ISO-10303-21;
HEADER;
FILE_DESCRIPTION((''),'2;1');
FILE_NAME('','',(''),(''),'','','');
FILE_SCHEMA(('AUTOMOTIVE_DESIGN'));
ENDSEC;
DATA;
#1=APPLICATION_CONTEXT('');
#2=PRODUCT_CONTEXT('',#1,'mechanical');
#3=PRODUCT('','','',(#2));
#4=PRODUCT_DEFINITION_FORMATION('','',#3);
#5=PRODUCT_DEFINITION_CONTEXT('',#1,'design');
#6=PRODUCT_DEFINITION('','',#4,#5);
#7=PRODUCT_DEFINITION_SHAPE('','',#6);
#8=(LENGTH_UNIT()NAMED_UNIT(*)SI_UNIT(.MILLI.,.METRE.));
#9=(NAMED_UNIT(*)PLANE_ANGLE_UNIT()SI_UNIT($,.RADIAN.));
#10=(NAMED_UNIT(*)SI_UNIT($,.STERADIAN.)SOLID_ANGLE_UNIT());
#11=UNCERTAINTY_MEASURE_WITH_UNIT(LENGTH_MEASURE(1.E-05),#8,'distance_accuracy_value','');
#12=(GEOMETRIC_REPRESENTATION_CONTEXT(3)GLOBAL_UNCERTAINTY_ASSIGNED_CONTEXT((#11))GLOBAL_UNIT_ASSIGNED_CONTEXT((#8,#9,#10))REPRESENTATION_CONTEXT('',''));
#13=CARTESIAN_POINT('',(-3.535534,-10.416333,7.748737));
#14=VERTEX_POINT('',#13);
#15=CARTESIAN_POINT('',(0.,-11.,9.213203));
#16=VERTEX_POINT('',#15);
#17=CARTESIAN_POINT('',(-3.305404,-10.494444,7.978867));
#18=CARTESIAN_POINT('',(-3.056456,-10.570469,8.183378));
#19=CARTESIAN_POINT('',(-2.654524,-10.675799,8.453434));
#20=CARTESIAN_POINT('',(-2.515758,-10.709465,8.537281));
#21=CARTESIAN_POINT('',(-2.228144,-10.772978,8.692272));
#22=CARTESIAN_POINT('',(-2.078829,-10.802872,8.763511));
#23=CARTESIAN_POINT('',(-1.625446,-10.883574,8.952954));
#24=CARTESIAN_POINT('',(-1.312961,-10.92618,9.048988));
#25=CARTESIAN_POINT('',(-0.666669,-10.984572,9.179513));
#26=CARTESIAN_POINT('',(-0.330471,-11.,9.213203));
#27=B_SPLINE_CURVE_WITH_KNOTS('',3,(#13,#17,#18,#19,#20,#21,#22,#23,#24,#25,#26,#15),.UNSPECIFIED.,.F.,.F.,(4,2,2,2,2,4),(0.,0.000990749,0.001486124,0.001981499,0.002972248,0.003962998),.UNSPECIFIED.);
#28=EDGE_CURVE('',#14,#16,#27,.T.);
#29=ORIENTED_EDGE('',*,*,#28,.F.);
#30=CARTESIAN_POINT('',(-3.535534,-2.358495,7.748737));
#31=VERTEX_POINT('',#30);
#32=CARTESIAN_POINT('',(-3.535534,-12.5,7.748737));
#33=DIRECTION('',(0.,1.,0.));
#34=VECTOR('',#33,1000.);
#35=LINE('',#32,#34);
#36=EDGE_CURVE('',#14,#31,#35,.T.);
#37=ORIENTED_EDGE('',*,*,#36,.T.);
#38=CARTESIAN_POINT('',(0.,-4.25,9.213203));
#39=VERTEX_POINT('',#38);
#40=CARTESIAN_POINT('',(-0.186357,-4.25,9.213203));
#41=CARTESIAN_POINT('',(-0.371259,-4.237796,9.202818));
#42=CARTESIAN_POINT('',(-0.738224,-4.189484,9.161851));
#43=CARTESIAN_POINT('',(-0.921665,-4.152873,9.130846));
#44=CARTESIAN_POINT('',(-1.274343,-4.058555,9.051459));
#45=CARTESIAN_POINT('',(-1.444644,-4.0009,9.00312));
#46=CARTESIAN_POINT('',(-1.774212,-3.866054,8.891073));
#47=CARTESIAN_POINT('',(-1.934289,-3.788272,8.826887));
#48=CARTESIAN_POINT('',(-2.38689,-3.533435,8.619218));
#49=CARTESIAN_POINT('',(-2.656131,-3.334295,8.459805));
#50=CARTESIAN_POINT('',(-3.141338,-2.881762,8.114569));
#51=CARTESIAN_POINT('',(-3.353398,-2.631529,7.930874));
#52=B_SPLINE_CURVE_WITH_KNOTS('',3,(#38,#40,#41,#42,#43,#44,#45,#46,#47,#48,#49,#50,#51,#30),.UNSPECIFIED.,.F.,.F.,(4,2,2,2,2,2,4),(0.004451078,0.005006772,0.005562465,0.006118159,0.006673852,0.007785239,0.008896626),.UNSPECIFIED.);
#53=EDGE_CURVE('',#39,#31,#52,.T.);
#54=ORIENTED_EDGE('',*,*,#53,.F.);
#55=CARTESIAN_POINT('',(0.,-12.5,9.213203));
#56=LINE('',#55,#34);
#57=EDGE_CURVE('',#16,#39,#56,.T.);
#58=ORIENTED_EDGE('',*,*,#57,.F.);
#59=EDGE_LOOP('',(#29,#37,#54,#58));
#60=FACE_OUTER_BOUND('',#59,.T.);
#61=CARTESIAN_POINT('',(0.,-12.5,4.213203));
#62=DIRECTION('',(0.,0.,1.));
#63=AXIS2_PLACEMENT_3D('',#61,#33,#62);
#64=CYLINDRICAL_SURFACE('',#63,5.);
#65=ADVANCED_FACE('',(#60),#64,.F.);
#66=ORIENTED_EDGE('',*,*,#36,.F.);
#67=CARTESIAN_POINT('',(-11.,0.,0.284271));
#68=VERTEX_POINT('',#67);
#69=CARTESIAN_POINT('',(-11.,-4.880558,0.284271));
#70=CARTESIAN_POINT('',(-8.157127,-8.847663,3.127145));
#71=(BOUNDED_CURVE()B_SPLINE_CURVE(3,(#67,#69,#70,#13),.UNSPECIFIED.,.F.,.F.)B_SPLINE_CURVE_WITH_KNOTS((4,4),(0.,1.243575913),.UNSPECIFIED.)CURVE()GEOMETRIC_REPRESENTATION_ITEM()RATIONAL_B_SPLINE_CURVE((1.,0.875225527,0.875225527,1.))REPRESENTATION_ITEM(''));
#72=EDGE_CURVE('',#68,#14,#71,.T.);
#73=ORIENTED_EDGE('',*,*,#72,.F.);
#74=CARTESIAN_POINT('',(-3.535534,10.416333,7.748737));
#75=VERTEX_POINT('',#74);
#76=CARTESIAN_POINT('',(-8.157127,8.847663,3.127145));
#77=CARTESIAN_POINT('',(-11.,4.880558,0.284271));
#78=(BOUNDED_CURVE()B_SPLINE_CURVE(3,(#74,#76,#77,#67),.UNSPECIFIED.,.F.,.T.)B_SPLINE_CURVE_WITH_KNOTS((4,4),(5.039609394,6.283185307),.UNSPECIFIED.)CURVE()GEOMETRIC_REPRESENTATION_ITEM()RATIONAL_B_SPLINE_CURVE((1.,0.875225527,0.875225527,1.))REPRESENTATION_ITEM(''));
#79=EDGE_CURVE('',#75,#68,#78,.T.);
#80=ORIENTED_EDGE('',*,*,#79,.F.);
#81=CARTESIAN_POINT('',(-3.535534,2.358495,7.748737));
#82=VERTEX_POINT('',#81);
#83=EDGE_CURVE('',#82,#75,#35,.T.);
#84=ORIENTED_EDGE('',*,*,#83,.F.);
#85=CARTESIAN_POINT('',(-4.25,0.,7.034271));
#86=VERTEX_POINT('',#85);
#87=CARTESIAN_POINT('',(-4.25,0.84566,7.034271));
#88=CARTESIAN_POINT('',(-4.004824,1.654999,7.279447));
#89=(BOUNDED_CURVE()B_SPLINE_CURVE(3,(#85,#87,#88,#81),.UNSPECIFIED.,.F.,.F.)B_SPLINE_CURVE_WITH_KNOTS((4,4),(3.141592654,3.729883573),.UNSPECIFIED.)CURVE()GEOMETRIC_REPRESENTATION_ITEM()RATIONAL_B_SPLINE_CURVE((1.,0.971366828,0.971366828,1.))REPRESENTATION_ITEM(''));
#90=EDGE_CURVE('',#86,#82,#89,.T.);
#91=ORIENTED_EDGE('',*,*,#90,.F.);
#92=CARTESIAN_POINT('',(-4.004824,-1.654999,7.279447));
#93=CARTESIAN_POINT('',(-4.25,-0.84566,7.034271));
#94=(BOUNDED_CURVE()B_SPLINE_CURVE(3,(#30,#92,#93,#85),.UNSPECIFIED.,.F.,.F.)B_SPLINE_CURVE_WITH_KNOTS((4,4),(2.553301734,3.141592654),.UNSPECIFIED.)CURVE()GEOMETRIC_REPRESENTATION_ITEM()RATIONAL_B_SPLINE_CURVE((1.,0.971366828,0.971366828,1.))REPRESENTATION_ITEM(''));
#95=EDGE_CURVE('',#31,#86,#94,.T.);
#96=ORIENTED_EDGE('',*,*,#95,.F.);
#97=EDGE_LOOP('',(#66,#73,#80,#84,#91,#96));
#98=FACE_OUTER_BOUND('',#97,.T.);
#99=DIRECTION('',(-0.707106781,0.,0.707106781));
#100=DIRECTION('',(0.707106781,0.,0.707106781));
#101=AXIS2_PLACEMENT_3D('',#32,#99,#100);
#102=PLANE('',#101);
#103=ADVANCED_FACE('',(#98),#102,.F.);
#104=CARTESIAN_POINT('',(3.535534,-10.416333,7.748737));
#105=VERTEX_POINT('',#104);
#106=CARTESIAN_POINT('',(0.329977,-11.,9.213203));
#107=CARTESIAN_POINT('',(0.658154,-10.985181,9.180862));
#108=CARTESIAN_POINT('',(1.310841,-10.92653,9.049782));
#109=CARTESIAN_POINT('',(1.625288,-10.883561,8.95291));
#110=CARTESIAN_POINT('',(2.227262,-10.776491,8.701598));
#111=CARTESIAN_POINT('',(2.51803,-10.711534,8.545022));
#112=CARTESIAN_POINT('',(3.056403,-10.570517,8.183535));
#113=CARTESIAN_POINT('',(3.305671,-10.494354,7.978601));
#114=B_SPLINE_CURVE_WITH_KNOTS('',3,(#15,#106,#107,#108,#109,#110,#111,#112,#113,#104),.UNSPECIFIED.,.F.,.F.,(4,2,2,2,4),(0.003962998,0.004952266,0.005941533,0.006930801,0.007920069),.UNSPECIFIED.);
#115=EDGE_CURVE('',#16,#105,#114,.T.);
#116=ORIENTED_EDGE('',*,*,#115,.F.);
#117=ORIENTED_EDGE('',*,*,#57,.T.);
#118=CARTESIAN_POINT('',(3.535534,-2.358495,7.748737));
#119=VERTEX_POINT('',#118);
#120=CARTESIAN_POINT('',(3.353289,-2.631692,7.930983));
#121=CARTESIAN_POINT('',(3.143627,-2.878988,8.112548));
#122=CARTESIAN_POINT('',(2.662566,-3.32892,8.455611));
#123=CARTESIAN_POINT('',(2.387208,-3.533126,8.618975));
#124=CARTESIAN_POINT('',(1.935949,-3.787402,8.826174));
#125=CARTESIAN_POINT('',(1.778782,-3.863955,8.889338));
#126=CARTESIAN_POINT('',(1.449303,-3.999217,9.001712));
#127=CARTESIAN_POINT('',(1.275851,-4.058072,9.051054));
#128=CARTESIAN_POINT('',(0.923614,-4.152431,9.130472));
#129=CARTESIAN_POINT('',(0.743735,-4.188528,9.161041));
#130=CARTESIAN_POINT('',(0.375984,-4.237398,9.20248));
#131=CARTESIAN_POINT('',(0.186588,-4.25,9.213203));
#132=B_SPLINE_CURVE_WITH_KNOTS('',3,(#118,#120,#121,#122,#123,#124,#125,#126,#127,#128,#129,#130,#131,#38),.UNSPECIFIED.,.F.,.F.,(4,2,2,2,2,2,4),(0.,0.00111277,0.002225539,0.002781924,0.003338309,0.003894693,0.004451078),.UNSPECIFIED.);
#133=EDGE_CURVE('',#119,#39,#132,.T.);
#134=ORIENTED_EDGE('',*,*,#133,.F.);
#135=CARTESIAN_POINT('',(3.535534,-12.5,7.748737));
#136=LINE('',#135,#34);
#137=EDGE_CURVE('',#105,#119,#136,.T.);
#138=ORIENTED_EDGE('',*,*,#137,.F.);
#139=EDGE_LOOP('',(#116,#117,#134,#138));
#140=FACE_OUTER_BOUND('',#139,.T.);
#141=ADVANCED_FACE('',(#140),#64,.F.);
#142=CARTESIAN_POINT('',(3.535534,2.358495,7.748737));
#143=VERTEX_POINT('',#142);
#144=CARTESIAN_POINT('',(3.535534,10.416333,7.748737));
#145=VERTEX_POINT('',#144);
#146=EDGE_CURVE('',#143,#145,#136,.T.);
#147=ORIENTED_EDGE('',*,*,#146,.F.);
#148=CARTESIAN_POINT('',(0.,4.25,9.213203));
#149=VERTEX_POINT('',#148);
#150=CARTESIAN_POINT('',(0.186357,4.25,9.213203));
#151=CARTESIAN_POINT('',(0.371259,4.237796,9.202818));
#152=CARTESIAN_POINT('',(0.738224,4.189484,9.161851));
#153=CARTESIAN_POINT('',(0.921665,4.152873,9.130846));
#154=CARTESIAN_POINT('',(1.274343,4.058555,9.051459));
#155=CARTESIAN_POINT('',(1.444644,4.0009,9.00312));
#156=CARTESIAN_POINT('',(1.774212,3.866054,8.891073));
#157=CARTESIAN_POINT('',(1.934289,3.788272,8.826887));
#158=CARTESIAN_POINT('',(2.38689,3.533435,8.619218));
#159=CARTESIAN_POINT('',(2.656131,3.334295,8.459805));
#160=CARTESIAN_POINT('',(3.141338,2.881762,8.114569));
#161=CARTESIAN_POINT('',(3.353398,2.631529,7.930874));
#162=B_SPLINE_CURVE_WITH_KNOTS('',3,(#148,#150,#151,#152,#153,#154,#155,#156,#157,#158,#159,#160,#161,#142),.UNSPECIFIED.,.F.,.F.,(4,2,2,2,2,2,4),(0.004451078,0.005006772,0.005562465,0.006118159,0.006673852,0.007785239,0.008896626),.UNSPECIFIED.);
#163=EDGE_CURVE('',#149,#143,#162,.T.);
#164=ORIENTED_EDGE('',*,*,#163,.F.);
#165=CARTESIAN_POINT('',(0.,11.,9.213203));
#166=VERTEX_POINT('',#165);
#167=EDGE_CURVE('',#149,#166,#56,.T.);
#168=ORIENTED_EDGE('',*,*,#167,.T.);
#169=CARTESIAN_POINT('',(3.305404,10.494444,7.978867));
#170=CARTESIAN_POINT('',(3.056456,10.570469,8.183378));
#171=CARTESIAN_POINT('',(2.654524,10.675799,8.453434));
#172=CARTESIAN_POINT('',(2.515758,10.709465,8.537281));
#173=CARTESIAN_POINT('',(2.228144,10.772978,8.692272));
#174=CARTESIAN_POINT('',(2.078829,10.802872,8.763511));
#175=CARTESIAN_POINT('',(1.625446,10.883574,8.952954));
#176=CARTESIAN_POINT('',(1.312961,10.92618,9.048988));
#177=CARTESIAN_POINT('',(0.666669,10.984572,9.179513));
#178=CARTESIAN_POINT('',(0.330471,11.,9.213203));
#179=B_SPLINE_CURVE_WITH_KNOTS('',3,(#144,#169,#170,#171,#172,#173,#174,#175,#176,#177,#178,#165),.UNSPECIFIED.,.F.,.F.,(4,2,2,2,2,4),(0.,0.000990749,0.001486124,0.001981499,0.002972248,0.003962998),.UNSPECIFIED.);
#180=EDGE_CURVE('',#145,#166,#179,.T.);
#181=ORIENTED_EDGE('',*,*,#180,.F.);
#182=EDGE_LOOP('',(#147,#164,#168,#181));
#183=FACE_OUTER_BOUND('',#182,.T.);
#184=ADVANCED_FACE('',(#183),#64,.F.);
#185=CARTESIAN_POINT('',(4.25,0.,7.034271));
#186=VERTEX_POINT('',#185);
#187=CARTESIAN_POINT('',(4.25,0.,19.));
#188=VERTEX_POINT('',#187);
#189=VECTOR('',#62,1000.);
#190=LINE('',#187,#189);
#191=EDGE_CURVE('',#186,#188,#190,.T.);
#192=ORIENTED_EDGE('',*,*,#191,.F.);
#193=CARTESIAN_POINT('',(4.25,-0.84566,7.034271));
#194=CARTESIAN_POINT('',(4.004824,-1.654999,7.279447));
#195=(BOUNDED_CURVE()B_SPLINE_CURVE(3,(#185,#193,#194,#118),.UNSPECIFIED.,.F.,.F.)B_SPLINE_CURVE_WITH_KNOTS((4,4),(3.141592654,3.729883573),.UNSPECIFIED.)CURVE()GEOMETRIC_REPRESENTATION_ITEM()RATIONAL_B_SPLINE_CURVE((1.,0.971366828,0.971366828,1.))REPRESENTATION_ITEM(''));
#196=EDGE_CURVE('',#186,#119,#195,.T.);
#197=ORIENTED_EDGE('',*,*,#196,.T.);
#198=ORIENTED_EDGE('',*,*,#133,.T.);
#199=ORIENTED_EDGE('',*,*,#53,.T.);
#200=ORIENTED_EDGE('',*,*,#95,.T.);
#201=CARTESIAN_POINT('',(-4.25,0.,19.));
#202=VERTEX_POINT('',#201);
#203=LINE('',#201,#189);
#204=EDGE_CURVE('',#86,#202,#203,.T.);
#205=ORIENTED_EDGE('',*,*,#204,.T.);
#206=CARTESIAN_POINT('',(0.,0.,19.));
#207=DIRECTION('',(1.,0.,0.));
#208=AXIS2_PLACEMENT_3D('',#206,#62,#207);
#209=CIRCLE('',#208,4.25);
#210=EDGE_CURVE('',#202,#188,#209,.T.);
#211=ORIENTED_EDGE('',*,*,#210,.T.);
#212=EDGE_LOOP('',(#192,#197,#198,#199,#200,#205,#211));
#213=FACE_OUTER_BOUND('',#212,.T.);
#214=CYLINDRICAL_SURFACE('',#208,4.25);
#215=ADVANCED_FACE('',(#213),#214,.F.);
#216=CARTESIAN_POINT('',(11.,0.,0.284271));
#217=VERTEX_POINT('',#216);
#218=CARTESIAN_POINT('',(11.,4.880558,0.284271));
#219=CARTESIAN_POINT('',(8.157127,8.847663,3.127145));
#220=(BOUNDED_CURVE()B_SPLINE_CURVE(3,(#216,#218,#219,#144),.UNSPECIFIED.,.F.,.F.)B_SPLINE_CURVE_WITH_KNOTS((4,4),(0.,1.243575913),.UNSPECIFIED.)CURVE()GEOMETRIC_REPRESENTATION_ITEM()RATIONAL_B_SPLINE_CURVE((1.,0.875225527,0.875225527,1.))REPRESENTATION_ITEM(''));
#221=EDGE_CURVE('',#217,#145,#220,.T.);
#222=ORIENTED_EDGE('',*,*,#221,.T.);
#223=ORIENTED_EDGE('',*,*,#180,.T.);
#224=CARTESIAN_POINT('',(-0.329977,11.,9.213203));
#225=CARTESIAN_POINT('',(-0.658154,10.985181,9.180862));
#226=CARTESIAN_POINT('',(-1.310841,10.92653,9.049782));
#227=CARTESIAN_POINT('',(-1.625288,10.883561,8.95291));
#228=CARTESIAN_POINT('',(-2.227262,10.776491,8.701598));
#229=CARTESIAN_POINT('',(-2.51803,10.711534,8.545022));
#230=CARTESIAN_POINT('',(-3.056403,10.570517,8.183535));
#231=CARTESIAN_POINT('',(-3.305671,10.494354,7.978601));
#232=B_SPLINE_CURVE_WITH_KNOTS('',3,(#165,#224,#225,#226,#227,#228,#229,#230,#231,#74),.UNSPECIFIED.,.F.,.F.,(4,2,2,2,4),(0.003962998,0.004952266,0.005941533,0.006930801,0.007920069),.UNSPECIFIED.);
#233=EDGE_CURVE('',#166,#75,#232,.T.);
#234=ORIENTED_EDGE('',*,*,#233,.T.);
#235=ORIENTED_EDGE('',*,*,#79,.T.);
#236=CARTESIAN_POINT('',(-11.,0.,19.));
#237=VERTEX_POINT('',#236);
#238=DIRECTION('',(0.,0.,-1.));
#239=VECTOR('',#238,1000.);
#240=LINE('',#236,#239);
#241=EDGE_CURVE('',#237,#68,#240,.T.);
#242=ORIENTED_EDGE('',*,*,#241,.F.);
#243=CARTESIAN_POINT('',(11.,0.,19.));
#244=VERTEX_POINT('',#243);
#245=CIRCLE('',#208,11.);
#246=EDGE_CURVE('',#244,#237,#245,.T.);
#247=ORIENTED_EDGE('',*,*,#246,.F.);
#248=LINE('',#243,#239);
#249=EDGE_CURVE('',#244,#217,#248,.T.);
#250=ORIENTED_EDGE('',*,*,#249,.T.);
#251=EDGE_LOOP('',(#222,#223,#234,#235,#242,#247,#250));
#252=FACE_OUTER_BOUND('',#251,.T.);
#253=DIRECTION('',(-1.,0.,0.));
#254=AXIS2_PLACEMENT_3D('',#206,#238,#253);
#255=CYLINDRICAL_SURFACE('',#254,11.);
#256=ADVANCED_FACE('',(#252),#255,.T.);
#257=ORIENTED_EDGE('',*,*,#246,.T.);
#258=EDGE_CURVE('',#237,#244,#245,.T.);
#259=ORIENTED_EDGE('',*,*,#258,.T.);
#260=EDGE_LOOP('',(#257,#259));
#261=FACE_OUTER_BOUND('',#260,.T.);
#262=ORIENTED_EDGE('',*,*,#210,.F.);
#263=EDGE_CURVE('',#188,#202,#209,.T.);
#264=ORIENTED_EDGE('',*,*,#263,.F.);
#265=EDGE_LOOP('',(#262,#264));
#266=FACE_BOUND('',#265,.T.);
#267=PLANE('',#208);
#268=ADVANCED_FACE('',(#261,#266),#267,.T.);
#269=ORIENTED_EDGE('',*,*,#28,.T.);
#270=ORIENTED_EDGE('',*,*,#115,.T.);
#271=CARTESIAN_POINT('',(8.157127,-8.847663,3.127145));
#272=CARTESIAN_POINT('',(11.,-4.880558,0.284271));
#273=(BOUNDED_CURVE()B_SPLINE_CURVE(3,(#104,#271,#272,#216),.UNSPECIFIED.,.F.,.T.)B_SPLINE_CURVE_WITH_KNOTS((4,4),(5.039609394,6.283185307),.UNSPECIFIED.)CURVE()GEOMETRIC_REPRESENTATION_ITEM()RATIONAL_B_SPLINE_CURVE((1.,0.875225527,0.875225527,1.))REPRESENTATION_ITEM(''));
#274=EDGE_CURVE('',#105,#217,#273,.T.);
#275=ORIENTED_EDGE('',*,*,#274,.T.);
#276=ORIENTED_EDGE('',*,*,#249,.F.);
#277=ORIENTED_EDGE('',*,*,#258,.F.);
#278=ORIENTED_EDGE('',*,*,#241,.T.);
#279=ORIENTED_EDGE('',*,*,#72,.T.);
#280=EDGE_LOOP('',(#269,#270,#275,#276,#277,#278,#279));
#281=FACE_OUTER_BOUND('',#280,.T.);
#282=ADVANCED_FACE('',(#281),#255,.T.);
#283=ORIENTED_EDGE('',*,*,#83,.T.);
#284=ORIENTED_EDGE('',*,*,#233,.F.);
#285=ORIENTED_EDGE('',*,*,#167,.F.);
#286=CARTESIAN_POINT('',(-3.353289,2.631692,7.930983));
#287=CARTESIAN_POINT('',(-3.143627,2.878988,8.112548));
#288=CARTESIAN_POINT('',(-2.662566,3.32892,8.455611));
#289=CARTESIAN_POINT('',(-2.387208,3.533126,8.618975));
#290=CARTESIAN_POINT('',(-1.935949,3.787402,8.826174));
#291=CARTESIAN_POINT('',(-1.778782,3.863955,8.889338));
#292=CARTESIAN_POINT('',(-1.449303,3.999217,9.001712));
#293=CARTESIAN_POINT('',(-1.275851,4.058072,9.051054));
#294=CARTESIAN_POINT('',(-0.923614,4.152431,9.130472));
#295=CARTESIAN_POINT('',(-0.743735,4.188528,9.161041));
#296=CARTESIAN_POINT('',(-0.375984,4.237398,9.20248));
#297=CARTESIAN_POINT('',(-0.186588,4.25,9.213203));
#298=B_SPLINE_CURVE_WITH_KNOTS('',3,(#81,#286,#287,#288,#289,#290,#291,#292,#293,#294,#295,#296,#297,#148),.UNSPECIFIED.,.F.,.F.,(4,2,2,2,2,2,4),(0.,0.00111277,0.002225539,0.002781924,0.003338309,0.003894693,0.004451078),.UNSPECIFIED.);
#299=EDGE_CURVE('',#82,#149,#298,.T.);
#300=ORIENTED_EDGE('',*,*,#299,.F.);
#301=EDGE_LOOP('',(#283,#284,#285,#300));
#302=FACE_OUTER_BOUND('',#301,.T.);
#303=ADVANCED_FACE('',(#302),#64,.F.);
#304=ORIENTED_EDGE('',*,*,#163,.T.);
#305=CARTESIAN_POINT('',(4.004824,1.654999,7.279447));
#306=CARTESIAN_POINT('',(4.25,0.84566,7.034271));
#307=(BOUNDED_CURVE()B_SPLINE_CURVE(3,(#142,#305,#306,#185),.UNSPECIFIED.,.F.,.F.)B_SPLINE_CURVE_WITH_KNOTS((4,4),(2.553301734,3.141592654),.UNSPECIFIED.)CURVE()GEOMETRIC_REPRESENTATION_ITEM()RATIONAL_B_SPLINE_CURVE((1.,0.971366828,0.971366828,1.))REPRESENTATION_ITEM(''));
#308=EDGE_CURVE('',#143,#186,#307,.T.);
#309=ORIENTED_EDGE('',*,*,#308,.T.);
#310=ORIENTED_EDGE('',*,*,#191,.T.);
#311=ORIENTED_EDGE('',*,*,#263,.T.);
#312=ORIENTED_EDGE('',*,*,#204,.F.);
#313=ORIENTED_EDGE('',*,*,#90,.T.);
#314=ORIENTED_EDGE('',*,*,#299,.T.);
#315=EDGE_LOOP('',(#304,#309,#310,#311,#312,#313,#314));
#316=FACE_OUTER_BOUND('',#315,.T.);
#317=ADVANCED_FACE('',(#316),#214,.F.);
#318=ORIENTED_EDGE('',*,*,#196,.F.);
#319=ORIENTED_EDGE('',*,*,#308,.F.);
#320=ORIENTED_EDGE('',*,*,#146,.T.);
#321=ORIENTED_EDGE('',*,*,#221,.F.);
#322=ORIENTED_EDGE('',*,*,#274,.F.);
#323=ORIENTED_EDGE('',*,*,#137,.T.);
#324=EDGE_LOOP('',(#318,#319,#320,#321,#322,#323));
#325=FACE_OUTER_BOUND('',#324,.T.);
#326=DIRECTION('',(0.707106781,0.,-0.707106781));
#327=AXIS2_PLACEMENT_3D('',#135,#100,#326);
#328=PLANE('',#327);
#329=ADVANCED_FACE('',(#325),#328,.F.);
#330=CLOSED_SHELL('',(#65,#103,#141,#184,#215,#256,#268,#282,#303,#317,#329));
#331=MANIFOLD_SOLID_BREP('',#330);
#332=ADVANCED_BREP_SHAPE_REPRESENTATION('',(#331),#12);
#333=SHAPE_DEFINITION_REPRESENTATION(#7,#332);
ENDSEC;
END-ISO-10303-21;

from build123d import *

# Parameters (mm, degrees)
SKETCH1_R              = 11
BOSS_EXTRUDE1_DEPTH    = 19
M10_TAPPED_HOLE1_D     = 8.5
M10_TAPPED_HOLE1_DEPTH = 24.5
M10_TAPPED_HOLE1_TIP   = 2.553657631
CUT_EXTRUDE1_DEPTH     = 12.5


with BuildPart() as part:
    # Sketch1 → Boss-Extrude1 (new body)
    with BuildSketch(Plane.XY):
        Circle(SKETCH1_R)
    extrude(amount=BOSS_EXTRUDE1_DEPTH)

    # M10 Tapped Hole1
    with Locations(Plane.XY.offset(19)):
        with Locations((0, 0)):
            Hole(M10_TAPPED_HOLE1_D / 2, depth=M10_TAPPED_HOLE1_DEPTH)
            with Locations((0, 0, -(M10_TAPPED_HOLE1_DEPTH + M10_TAPPED_HOLE1_TIP / 2))):  # 118° drill point
                Cone(0, M10_TAPPED_HOLE1_D / 2, M10_TAPPED_HOLE1_TIP, mode=Mode.SUBTRACT)

    # Sketch4 → Cut-Extrude1 (cut, symmetric)
    with BuildSketch(Plane(origin=(0, 0, 0), x_dir=(1, 0, 0), z_dir=(0, 1, 0))):
        with BuildLine():
            Line((3.535533906, -7.748737342), (28.284271247, 17))
            Line((28.284271247, 17), (0, 45.284271247))
            Line((0, 45.284271247), (-28.284271247, 17))
            Line((-28.284271247, 17), (-3.535533906, -7.748737342))
            ThreePointArc((-3.535533906, -7.748737342), (0, -9.213203436), (3.535533906, -7.748737342))
        make_face()
    extrude(amount=CUT_EXTRUDE1_DEPTH, both=True, mode=Mode.SUBTRACT)


solid = part.part
